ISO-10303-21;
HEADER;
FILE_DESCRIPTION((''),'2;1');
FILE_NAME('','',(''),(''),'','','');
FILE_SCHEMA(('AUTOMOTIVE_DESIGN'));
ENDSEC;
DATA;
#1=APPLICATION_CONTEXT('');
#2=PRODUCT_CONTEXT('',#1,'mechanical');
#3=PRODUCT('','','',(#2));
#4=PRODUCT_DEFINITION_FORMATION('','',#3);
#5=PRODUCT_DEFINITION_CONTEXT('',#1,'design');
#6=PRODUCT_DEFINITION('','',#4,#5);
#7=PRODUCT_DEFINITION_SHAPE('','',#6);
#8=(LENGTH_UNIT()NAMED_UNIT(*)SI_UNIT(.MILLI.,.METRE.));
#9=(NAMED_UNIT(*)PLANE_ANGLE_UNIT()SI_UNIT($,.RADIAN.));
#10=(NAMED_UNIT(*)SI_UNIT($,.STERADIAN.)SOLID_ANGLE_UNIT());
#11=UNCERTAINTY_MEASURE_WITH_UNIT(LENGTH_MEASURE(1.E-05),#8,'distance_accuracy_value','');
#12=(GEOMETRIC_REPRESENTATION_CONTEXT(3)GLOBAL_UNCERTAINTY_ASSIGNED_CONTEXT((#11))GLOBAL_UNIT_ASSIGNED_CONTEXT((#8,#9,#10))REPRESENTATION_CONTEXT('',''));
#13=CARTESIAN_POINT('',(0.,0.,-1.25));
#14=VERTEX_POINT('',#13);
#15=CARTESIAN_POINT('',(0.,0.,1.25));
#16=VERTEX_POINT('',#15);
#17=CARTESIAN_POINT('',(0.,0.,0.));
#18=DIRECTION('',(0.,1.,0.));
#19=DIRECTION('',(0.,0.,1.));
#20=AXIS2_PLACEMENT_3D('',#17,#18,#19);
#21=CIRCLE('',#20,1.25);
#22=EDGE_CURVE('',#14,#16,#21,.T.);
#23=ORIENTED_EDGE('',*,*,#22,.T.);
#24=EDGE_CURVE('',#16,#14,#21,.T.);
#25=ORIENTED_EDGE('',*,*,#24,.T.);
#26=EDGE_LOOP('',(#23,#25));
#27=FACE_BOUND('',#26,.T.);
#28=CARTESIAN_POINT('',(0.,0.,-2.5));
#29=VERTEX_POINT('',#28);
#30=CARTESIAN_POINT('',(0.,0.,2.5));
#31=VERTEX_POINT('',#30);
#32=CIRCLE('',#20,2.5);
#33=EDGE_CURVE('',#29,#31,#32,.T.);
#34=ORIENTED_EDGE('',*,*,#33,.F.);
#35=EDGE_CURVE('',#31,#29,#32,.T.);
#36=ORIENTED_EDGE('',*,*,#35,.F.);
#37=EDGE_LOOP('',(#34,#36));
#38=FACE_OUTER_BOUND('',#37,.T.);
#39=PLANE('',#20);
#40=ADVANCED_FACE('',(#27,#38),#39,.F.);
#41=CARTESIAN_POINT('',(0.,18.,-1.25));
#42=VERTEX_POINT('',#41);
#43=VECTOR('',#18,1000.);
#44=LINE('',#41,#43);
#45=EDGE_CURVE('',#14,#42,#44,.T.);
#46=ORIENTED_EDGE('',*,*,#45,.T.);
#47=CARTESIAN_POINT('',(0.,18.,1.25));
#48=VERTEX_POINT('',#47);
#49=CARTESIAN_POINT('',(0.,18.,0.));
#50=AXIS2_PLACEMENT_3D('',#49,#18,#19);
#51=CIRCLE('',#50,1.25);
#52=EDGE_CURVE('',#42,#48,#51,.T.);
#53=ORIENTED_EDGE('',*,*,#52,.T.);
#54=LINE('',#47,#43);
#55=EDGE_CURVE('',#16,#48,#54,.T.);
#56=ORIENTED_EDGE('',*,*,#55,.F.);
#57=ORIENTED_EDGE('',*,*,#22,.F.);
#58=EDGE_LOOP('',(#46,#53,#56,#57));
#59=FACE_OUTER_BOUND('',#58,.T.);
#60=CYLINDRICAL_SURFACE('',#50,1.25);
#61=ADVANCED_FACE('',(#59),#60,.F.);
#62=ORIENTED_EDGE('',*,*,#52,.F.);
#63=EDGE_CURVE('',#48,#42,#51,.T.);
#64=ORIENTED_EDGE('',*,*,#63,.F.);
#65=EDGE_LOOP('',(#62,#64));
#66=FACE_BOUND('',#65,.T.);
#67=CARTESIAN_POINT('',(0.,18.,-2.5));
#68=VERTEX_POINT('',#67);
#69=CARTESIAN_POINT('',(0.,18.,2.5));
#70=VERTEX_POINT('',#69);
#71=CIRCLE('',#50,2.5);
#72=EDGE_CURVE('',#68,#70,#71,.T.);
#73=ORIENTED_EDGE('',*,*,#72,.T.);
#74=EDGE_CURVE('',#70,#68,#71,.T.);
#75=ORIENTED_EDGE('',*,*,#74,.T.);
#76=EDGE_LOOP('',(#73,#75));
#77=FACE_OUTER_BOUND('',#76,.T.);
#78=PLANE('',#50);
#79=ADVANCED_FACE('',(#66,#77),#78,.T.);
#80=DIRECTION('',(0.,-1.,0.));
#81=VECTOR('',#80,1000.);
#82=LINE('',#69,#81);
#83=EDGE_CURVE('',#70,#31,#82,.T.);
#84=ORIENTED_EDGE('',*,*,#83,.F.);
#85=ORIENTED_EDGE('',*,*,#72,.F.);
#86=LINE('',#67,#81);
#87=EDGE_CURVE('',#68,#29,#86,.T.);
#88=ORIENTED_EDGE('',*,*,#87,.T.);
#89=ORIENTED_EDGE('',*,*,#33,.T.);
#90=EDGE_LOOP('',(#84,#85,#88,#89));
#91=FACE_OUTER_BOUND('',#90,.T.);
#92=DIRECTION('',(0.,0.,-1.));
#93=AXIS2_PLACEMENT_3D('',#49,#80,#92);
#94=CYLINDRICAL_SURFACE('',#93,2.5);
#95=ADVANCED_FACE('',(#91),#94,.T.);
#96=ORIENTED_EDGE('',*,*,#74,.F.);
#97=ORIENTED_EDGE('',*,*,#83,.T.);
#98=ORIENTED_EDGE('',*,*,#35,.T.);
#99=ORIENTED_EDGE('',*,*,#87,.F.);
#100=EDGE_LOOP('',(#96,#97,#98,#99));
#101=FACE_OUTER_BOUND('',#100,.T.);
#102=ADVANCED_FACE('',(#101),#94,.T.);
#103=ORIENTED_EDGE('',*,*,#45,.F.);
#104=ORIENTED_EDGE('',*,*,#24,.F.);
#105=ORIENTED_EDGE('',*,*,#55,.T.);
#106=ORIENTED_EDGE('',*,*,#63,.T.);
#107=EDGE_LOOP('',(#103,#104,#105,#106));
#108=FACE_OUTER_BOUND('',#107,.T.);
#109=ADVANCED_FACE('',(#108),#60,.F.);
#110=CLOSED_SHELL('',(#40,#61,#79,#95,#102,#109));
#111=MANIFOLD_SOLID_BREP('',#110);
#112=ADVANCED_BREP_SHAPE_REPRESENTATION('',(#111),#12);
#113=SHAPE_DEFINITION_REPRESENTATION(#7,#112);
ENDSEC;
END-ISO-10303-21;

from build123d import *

# Parameters (mm, degrees)
SKETCH_1_R         = 2.5
EXTRUDE_1_DEPTH    = 18
HOLE_WIZARD_M3_1_D = 2.5


with BuildPart() as part:
    # 草图1 → 凸台-拉伸1 (new body)
    with BuildSketch(Plane(origin=(0, 0, 0), x_dir=(1, 0, 0), z_dir=(0, 1, 0))):
        with Locations(Location((0, 0, 0), (0, 0, 270))):
            Circle(SKETCH_1_R)
    extrude(amount=EXTRUDE_1_DEPTH)

    # M3 螺纹孔1 (through all)
    with Locations(Plane(origin=(0, 18, 0), x_dir=(1, 0, 0), z_dir=(0, 1, 0))):
        with Locations((0, 0)):
            Hole(HOLE_WIZARD_M3_1_D / 2)


solid = part.part
